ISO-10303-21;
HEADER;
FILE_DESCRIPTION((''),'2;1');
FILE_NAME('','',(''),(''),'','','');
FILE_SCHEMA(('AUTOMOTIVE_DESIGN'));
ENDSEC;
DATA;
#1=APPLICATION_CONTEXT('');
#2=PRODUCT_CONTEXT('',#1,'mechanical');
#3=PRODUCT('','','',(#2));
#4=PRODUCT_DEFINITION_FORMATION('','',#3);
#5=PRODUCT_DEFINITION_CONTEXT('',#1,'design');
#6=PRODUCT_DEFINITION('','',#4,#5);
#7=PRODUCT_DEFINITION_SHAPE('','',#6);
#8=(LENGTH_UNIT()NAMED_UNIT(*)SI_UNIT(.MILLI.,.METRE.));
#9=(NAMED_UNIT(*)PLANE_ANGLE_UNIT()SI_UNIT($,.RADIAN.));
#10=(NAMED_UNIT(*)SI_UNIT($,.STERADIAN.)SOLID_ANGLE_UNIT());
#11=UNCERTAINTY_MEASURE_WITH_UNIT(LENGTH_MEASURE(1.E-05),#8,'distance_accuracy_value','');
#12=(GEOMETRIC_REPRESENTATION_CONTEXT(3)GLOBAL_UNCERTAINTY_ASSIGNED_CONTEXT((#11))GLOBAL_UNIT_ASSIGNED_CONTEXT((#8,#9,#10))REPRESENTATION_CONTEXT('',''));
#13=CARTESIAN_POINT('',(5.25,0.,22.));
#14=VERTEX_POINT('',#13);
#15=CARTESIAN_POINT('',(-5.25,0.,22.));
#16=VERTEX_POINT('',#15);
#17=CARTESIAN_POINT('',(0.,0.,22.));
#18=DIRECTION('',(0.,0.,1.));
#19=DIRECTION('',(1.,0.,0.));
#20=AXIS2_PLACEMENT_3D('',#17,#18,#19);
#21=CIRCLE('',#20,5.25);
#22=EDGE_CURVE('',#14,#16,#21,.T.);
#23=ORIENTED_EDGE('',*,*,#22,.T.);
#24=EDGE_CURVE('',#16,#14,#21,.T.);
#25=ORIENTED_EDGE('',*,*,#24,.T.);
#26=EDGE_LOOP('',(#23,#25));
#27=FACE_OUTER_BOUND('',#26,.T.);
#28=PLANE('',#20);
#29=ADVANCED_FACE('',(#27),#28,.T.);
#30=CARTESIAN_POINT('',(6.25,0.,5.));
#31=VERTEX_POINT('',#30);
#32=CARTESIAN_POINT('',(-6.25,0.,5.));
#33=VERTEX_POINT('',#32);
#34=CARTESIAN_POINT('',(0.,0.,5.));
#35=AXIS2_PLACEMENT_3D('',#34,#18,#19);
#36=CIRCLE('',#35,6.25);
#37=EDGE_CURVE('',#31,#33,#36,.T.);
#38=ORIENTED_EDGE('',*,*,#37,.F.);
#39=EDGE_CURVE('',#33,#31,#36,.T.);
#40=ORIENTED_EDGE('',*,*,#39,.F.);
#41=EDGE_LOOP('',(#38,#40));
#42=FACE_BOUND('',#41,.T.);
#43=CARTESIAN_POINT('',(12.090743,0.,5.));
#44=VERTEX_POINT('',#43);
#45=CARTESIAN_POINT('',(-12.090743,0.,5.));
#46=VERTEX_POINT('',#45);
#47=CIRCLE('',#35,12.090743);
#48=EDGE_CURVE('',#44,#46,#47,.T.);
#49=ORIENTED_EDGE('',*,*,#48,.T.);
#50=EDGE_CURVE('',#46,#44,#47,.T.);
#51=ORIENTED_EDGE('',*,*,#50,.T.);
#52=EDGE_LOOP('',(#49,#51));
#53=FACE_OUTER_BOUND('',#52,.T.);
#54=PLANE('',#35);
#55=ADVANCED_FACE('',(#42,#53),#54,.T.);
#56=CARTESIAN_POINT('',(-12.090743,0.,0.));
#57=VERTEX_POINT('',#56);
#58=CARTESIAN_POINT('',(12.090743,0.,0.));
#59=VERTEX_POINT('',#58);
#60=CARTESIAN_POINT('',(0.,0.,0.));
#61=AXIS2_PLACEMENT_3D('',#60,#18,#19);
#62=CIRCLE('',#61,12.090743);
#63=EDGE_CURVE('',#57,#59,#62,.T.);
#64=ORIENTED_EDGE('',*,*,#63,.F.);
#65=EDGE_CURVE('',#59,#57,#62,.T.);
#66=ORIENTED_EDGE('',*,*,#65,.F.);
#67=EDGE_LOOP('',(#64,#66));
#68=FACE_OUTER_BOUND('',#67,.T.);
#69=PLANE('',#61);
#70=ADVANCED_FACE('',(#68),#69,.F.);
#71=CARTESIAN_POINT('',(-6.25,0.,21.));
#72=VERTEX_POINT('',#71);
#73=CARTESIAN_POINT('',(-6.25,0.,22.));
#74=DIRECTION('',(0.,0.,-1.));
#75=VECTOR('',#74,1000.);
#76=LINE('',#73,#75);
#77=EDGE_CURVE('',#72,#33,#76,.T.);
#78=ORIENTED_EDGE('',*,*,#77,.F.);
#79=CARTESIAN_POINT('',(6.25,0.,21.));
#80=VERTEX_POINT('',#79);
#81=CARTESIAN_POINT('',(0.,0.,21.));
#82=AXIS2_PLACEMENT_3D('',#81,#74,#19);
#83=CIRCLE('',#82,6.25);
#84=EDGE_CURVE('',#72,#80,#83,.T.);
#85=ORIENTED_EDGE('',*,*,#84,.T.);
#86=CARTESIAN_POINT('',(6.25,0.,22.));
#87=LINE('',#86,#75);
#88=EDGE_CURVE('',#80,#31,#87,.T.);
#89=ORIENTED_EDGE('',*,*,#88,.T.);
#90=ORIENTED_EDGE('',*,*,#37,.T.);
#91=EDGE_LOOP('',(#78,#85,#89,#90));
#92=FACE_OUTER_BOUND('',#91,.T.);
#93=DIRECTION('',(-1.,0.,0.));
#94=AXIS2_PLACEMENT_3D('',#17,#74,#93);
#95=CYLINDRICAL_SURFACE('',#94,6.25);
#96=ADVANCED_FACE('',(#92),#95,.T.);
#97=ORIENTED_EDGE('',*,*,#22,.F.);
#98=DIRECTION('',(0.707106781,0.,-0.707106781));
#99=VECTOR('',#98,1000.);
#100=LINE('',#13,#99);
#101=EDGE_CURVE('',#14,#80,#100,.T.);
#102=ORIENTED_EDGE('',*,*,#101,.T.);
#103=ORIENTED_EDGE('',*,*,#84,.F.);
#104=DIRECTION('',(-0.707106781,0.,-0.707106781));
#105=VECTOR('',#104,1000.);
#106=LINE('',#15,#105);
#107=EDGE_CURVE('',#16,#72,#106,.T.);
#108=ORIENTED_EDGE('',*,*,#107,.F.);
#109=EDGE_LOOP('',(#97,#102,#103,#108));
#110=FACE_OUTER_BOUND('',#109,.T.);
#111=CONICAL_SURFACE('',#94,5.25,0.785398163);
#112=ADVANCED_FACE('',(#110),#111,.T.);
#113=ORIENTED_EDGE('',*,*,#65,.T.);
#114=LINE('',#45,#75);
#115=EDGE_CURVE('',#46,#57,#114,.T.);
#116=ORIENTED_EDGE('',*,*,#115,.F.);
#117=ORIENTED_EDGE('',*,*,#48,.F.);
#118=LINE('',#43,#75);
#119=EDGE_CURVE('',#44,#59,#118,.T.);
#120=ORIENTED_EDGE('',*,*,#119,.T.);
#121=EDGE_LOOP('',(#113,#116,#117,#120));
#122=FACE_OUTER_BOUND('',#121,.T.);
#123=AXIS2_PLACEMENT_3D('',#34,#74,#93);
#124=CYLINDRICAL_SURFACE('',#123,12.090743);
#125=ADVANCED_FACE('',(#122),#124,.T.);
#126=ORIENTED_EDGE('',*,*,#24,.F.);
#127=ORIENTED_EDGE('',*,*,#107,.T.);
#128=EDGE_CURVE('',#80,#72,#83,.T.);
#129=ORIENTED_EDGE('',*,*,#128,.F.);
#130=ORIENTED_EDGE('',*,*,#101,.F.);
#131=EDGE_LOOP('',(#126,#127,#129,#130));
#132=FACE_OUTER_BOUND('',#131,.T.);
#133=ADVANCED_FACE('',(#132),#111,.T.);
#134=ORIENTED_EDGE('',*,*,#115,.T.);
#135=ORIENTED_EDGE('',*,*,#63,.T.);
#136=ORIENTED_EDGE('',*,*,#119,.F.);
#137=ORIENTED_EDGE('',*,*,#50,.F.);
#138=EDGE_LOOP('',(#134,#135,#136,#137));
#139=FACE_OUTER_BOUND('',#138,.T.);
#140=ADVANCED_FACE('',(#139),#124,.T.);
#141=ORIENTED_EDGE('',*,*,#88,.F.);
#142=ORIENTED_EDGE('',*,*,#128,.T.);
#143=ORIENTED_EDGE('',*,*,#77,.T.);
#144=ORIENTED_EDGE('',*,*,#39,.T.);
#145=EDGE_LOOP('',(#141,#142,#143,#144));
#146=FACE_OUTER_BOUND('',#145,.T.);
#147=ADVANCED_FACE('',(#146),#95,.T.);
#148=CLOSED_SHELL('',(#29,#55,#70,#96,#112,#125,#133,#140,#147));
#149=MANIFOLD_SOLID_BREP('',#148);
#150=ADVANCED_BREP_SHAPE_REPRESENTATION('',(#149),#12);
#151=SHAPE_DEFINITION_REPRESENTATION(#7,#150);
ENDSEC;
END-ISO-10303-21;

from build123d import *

# Parameters (mm, degrees)
SKETCH1_R           = 12.090742714
BOSS_EXTRUDE1_DEPTH = 5
SKETCH2_R           = 6.25
BOSS_EXTRUDE2_DEPTH = 17
CHAMFER1_SIZE       = 1


with BuildPart() as part:
    # Sketch1 → Boss-Extrude1 (new body)
    with BuildSketch(Plane.XY):
        Circle(SKETCH1_R)
    extrude(amount=BOSS_EXTRUDE1_DEPTH)

    # Sketch2 → Boss-Extrude2 (add)
    with BuildSketch(Plane.XY.offset(5)):
        Circle(SKETCH2_R)
    extrude(amount=BOSS_EXTRUDE2_DEPTH)

    # Chamfer1
    chamfer1_edges = [part.edges().sort_by_distance(p)[0] for p in [
        (-6.25, 0, 22),
    ]]
    chamfer(chamfer1_edges, length=CHAMFER1_SIZE)


solid = part.part
